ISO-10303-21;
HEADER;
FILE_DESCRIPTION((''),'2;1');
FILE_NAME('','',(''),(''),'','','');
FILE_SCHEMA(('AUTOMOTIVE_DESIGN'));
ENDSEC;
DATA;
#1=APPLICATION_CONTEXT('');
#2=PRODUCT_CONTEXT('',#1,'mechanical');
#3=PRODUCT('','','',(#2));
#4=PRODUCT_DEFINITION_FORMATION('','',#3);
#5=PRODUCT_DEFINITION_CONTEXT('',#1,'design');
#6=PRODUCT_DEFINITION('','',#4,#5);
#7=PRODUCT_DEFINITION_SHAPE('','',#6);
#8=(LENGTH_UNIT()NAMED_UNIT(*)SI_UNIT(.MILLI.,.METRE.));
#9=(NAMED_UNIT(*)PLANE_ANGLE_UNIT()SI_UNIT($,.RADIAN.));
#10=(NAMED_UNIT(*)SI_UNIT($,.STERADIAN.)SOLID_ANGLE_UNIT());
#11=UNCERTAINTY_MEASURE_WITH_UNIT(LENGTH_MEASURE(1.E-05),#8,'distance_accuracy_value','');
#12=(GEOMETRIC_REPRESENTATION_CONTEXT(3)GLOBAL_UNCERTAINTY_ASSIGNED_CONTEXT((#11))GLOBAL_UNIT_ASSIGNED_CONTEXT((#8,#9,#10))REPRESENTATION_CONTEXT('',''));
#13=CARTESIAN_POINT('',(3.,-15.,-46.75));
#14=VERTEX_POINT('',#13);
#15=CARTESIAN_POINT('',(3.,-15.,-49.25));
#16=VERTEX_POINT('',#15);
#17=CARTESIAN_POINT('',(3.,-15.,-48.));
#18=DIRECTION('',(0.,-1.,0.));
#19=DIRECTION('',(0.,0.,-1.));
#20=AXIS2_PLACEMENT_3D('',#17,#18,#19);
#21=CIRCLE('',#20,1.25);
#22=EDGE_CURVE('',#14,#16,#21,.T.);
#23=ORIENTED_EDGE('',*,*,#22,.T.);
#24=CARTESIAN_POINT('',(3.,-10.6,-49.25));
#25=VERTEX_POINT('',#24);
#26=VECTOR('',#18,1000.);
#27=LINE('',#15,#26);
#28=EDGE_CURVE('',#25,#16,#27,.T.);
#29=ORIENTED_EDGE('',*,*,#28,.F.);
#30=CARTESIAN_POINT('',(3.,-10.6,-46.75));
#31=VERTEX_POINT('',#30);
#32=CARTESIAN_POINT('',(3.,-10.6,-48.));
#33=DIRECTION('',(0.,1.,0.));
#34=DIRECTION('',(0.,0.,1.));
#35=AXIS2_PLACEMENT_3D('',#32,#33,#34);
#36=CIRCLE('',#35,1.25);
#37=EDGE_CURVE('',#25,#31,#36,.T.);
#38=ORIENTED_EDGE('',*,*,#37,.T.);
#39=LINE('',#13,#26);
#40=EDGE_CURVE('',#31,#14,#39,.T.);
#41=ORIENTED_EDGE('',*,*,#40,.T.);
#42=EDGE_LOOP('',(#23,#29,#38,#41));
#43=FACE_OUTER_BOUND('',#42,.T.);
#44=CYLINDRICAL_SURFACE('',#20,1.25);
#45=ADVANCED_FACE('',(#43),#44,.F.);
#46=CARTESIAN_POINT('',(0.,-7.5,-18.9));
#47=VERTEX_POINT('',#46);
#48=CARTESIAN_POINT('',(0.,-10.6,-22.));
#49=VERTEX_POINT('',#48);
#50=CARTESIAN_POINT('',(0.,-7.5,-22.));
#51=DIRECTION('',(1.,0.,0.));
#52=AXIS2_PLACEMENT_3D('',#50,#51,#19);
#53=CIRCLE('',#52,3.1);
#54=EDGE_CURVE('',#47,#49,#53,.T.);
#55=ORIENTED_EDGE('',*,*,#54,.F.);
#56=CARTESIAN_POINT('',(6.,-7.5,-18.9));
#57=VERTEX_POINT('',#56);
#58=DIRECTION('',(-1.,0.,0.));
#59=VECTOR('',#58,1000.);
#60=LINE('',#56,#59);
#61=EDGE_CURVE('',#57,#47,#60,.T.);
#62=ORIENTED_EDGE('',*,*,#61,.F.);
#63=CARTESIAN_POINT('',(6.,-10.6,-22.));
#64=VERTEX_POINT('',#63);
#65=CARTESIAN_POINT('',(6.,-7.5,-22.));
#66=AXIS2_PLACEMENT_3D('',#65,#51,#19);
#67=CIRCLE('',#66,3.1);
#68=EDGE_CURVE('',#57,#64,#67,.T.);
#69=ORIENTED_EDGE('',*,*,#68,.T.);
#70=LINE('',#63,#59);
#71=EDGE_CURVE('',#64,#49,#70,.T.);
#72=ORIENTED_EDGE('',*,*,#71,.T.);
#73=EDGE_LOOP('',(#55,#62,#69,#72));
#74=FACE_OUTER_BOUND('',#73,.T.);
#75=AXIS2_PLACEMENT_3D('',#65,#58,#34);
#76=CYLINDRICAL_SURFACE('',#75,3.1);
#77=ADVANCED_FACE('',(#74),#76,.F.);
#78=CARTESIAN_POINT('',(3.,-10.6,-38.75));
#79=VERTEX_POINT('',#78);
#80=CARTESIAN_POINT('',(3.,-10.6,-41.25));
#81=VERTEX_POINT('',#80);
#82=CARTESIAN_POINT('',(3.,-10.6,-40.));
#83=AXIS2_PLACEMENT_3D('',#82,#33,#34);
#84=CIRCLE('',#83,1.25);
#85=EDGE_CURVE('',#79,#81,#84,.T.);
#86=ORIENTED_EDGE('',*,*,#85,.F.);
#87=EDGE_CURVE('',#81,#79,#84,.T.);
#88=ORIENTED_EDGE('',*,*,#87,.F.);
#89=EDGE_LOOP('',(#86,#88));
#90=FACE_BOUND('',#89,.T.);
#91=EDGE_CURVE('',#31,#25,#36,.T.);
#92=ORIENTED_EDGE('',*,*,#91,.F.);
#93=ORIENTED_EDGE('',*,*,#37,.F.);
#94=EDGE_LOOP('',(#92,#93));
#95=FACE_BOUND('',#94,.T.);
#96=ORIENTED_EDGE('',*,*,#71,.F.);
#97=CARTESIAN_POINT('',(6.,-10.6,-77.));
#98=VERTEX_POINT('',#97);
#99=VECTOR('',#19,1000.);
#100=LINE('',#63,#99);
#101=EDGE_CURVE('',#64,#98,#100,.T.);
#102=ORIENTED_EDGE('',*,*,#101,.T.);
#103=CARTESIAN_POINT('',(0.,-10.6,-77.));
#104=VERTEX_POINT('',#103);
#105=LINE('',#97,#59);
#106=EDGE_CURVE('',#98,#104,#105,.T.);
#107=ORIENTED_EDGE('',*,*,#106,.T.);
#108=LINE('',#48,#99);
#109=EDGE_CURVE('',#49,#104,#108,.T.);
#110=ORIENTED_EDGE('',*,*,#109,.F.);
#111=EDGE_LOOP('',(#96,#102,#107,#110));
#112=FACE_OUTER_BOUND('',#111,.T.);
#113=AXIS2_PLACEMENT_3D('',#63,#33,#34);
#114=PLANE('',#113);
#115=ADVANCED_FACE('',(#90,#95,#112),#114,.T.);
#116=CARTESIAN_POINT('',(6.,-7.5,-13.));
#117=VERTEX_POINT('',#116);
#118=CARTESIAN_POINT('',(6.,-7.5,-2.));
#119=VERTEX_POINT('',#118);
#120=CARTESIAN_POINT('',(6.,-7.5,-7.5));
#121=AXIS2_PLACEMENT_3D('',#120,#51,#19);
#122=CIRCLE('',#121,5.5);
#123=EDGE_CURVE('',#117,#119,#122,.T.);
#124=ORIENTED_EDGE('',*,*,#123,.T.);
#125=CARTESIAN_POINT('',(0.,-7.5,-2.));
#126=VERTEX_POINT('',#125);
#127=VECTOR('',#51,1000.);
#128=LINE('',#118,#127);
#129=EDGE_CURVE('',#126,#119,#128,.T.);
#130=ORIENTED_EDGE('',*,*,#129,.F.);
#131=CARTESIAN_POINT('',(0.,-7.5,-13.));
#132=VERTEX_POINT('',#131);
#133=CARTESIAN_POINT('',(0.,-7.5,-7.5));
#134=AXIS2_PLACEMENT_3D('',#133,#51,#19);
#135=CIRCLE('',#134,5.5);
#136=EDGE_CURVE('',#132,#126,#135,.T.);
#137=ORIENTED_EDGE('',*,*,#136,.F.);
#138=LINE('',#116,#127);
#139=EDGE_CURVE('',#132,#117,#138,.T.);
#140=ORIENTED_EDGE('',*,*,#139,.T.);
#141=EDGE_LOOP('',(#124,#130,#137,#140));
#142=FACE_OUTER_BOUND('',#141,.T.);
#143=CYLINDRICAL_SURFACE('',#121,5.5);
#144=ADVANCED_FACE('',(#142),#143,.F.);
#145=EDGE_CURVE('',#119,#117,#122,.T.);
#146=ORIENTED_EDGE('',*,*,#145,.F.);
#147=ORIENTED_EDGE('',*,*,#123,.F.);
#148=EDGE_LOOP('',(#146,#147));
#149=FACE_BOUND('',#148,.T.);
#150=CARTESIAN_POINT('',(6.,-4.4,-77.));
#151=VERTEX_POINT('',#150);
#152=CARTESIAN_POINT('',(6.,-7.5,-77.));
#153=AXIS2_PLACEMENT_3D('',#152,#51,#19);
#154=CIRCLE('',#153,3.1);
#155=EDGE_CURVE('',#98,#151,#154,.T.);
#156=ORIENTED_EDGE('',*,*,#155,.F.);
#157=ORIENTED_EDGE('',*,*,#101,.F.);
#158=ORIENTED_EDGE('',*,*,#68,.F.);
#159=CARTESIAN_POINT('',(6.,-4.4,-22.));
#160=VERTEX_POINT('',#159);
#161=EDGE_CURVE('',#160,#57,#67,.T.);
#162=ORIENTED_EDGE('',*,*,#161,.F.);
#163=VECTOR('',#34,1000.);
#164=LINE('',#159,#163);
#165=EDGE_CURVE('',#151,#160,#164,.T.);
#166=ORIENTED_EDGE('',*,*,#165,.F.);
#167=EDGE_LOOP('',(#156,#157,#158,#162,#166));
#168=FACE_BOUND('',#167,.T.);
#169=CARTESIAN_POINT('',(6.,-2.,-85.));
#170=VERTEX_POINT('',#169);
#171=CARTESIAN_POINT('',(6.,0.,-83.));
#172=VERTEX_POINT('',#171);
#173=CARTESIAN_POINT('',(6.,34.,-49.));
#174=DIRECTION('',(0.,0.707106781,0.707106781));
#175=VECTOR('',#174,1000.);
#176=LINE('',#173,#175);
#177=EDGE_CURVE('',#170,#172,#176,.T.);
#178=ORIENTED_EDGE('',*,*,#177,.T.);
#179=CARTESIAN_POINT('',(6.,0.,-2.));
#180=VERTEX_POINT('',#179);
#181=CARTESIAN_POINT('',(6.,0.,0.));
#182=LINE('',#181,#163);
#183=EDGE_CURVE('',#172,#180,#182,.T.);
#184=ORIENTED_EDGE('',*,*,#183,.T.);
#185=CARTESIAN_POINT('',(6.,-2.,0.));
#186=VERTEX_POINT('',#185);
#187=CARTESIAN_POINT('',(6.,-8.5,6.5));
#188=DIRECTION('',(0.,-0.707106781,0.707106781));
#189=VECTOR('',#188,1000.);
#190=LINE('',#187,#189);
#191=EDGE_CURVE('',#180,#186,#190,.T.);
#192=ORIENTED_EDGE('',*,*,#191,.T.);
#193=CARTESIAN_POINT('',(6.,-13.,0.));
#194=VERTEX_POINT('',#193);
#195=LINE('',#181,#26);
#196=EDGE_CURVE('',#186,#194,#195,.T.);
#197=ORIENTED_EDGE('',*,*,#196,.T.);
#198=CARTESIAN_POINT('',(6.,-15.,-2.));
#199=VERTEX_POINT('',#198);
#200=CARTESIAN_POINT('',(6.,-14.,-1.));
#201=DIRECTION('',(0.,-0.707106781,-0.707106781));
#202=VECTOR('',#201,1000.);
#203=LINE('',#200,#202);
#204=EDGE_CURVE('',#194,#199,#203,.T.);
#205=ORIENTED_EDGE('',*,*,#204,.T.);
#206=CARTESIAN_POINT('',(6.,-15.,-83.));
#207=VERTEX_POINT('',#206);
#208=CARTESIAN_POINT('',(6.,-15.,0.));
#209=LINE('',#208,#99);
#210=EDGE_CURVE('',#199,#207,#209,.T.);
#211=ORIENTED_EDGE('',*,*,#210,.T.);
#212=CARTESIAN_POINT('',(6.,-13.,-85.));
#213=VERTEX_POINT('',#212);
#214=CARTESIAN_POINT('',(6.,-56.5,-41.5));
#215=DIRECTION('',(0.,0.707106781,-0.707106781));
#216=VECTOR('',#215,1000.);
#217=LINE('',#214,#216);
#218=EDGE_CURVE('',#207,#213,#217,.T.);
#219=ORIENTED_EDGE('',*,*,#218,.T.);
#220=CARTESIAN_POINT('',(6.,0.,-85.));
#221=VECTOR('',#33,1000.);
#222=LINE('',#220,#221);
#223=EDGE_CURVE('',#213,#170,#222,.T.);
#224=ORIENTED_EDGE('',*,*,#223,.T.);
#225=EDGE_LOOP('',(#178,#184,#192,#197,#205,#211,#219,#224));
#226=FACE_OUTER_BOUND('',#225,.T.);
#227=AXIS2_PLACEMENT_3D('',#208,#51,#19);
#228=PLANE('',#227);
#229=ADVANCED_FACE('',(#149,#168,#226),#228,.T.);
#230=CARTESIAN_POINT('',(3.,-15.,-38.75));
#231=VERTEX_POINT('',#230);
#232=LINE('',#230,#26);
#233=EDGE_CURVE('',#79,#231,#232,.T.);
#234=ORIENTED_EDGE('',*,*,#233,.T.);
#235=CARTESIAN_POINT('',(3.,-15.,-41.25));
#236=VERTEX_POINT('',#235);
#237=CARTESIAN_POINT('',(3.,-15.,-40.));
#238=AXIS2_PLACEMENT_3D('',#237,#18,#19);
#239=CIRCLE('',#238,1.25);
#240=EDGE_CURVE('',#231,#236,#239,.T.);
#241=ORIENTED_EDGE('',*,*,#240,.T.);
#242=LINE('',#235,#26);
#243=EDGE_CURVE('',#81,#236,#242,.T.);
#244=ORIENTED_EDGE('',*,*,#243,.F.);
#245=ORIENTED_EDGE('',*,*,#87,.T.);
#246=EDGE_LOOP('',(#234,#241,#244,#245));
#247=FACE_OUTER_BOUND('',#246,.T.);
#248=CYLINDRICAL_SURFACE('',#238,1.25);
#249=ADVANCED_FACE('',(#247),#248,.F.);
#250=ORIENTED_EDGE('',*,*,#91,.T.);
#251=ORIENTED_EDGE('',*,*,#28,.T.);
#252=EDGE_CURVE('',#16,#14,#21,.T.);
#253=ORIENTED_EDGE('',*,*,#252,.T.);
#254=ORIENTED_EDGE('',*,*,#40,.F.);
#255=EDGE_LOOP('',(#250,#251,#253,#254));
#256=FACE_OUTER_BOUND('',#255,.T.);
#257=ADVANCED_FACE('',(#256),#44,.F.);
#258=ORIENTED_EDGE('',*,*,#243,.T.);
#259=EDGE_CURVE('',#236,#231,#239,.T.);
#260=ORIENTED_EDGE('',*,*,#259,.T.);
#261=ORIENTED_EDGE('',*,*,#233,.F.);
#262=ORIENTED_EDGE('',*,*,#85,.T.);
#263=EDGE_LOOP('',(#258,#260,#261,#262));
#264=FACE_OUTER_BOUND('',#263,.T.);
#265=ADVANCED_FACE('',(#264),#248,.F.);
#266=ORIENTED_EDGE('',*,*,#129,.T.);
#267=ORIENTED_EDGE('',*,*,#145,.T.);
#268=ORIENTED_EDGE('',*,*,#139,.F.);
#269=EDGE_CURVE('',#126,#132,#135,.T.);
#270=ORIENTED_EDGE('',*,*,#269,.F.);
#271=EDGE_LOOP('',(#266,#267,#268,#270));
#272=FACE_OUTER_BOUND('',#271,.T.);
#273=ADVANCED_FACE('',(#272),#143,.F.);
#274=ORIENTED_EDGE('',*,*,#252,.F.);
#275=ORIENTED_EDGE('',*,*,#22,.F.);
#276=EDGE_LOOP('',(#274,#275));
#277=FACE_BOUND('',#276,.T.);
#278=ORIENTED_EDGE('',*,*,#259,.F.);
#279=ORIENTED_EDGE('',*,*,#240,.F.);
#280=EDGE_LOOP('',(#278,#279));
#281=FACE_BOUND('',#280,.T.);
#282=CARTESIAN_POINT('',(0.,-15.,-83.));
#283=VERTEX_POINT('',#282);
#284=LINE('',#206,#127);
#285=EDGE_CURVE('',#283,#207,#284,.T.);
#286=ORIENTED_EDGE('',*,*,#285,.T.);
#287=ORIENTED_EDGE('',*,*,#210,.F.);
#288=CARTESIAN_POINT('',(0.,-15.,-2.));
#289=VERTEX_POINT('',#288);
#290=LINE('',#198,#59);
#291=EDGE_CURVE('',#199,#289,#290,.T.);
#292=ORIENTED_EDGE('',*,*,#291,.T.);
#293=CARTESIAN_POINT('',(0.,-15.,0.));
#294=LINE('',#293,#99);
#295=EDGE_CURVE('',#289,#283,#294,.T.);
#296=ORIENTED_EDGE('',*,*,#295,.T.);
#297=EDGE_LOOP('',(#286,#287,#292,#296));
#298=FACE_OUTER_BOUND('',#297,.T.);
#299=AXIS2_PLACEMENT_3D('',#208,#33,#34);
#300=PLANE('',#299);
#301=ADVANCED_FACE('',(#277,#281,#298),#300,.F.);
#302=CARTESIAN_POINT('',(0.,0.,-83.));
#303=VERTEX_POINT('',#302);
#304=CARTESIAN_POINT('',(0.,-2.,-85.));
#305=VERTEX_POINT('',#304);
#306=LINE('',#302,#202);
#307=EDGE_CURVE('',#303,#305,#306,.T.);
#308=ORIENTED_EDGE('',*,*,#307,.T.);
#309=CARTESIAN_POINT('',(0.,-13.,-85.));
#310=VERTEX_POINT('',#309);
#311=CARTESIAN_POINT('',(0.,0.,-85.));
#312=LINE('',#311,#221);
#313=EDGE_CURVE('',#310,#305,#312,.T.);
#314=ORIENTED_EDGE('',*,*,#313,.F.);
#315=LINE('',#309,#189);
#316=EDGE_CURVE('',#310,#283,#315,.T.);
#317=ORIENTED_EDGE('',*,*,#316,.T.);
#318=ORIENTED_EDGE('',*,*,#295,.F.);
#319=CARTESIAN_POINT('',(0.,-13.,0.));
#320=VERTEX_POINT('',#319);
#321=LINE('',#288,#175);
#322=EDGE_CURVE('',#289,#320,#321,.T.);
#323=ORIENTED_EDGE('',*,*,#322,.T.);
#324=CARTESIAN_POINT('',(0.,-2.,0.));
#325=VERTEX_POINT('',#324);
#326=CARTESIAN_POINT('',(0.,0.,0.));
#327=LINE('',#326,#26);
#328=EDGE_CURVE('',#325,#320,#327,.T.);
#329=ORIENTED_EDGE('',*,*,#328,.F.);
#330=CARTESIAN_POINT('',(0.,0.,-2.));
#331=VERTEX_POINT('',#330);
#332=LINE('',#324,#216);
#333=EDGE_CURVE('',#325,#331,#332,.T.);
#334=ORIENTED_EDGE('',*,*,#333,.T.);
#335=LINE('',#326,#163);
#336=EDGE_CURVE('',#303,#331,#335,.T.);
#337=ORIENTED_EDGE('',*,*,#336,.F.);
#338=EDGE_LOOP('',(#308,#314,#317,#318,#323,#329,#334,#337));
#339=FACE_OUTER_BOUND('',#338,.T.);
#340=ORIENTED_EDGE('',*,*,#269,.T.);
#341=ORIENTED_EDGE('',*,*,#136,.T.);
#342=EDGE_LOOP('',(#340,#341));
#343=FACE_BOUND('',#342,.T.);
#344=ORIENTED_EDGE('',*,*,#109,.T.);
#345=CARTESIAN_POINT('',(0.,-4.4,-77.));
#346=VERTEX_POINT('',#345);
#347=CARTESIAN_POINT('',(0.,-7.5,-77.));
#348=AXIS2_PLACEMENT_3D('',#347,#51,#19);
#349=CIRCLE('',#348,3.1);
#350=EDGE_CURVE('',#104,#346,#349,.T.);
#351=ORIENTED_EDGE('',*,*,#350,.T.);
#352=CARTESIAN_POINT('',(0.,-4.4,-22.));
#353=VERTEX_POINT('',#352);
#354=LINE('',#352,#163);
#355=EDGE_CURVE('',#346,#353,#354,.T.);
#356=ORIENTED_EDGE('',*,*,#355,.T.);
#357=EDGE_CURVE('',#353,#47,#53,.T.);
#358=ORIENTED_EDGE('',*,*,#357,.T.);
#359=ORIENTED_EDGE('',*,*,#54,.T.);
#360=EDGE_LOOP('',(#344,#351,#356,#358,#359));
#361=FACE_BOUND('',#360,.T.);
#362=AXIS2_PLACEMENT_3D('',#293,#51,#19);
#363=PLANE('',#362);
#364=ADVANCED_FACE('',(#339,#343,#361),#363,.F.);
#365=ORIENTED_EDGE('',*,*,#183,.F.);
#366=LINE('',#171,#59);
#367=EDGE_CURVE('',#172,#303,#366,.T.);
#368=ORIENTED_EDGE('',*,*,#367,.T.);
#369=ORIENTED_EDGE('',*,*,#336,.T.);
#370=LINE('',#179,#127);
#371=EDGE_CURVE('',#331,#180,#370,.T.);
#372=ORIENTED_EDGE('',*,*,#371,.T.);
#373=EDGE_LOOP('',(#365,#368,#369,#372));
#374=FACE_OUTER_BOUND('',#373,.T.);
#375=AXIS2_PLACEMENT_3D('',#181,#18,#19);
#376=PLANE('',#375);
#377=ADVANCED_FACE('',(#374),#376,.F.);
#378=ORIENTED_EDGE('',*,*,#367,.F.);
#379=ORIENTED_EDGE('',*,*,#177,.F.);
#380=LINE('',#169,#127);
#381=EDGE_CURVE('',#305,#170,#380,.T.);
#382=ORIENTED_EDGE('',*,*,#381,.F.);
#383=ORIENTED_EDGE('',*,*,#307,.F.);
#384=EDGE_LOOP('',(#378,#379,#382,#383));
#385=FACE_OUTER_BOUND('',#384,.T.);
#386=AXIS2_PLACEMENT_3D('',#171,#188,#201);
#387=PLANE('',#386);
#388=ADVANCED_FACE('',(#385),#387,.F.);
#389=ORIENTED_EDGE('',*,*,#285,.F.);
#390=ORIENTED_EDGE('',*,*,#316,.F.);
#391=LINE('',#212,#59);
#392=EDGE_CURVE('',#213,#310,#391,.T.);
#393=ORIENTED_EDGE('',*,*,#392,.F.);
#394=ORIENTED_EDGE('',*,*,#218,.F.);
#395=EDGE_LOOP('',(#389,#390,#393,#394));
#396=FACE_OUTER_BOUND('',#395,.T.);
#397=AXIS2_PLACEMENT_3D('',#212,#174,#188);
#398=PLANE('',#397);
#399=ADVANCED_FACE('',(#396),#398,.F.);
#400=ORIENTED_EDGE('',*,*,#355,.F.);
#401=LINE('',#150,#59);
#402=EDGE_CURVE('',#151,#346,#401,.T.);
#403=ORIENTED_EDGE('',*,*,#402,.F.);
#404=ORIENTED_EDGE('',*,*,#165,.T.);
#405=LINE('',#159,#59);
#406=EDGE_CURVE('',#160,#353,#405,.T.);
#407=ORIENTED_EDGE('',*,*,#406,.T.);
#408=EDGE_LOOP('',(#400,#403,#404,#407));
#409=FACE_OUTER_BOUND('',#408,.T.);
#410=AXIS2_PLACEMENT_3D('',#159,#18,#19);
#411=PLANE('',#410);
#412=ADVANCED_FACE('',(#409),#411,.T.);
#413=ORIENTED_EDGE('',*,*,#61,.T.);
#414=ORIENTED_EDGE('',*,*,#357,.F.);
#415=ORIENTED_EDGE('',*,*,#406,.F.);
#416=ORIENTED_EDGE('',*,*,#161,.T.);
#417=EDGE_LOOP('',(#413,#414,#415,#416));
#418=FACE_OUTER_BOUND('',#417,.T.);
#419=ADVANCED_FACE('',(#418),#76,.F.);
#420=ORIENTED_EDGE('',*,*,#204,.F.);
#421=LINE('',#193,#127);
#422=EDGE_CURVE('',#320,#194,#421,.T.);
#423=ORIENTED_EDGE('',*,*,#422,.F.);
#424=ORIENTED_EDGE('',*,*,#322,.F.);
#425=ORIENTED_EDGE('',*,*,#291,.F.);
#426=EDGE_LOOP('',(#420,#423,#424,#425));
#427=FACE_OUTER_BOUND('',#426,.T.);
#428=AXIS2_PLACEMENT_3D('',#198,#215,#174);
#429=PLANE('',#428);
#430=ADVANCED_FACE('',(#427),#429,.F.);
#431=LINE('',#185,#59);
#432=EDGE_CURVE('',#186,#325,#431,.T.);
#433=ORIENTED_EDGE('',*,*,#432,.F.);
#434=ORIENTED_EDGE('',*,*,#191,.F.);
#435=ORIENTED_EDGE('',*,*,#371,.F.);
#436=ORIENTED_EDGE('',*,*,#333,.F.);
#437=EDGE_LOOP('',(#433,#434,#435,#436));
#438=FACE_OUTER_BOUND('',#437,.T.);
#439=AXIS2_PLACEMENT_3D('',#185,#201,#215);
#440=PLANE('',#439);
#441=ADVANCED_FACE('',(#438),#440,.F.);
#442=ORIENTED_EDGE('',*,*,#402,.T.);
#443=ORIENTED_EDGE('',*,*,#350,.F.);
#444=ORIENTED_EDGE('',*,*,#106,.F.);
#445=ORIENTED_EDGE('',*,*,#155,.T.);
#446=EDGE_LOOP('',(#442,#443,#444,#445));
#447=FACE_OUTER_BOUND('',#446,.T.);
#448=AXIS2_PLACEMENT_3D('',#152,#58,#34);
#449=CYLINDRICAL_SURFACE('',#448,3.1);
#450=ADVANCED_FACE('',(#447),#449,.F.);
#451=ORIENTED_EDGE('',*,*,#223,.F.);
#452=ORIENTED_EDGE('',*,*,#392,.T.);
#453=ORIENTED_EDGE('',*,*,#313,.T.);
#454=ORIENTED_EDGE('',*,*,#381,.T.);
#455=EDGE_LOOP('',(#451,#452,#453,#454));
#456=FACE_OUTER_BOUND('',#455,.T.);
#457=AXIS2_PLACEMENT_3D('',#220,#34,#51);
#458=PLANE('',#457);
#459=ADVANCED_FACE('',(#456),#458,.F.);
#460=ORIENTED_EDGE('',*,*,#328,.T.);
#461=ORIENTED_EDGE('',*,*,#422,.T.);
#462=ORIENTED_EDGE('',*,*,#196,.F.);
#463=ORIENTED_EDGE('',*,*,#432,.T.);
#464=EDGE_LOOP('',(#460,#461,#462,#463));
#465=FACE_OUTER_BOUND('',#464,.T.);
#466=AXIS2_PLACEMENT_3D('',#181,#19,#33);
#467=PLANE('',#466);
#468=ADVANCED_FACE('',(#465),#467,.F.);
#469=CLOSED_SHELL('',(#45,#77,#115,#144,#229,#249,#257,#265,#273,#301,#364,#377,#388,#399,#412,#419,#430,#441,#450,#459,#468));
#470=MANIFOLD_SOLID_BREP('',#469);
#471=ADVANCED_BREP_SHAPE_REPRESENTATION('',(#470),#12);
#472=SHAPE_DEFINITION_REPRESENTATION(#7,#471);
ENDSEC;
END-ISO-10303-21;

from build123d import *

# Parameters (mm, degrees)
SKETCH1_W              = 85
SKETCH1_H              = 15
EXTRUDE1_DEPTH         = 6
M12X1_0_TAPPED_HOLE1_D = 11
CHAMFER1_SIZE          = 2
M3_TAPPED_HOLE1_D      = 2.5
M3_TAPPED_HOLE1_DEPTH  = 8.5
M3_TAPPED_HOLE1_TIP    = 0.751075774


with BuildPart() as part:
    # Sketch1 → Extrude1 (new body)
    with BuildSketch(Plane(origin=(0, 0, 0), x_dir=(0, 0, -1), z_dir=(1, 0, 0))):
        with Locations((42.5, -7.5)):
            Rectangle(SKETCH1_W, SKETCH1_H)
        with BuildLine():
            Line((22, -4.4), (77, -4.4))
            ThreePointArc((77, -4.4), (80.1, -7.5), (77, -10.6))
            Line((77, -10.6), (22, -10.6))
            ThreePointArc((22, -10.6), (18.9, -7.5), (22, -4.4))
        make_face(mode=Mode.SUBTRACT)
    extrude(amount=EXTRUDE1_DEPTH)

    # M12x1.0 Tapped Hole1 (through all)
    with Locations(Plane(origin=(6, 0, 0), x_dir=(0, 0, -1), z_dir=(1, 0, 0))):
        with Locations((7.5, -7.5)):
            Hole(M12X1_0_TAPPED_HOLE1_D / 2)

    # Chamfer1
    chamfer1_edges = [part.edges().sort_by_distance(p)[0] for p in [
        (3, 0, 0),
        (3, 0, -85),
        (3, -15, -85),
        (3, -15, 0),
    ]]
    chamfer(chamfer1_edges, length=CHAMFER1_SIZE)

    # M3 Tapped Hole1
    with Locations(Plane.XZ.offset(15)):
        with Locations((3, -40), (3, -48)):
            Hole(M3_TAPPED_HOLE1_D / 2, depth=M3_TAPPED_HOLE1_DEPTH)
            with Locations((0, 0, -(M3_TAPPED_HOLE1_DEPTH + M3_TAPPED_HOLE1_TIP / 2))):  # 118° drill point
                Cone(0, M3_TAPPED_HOLE1_D / 2, M3_TAPPED_HOLE1_TIP, mode=Mode.SUBTRACT)


solid = part.part
